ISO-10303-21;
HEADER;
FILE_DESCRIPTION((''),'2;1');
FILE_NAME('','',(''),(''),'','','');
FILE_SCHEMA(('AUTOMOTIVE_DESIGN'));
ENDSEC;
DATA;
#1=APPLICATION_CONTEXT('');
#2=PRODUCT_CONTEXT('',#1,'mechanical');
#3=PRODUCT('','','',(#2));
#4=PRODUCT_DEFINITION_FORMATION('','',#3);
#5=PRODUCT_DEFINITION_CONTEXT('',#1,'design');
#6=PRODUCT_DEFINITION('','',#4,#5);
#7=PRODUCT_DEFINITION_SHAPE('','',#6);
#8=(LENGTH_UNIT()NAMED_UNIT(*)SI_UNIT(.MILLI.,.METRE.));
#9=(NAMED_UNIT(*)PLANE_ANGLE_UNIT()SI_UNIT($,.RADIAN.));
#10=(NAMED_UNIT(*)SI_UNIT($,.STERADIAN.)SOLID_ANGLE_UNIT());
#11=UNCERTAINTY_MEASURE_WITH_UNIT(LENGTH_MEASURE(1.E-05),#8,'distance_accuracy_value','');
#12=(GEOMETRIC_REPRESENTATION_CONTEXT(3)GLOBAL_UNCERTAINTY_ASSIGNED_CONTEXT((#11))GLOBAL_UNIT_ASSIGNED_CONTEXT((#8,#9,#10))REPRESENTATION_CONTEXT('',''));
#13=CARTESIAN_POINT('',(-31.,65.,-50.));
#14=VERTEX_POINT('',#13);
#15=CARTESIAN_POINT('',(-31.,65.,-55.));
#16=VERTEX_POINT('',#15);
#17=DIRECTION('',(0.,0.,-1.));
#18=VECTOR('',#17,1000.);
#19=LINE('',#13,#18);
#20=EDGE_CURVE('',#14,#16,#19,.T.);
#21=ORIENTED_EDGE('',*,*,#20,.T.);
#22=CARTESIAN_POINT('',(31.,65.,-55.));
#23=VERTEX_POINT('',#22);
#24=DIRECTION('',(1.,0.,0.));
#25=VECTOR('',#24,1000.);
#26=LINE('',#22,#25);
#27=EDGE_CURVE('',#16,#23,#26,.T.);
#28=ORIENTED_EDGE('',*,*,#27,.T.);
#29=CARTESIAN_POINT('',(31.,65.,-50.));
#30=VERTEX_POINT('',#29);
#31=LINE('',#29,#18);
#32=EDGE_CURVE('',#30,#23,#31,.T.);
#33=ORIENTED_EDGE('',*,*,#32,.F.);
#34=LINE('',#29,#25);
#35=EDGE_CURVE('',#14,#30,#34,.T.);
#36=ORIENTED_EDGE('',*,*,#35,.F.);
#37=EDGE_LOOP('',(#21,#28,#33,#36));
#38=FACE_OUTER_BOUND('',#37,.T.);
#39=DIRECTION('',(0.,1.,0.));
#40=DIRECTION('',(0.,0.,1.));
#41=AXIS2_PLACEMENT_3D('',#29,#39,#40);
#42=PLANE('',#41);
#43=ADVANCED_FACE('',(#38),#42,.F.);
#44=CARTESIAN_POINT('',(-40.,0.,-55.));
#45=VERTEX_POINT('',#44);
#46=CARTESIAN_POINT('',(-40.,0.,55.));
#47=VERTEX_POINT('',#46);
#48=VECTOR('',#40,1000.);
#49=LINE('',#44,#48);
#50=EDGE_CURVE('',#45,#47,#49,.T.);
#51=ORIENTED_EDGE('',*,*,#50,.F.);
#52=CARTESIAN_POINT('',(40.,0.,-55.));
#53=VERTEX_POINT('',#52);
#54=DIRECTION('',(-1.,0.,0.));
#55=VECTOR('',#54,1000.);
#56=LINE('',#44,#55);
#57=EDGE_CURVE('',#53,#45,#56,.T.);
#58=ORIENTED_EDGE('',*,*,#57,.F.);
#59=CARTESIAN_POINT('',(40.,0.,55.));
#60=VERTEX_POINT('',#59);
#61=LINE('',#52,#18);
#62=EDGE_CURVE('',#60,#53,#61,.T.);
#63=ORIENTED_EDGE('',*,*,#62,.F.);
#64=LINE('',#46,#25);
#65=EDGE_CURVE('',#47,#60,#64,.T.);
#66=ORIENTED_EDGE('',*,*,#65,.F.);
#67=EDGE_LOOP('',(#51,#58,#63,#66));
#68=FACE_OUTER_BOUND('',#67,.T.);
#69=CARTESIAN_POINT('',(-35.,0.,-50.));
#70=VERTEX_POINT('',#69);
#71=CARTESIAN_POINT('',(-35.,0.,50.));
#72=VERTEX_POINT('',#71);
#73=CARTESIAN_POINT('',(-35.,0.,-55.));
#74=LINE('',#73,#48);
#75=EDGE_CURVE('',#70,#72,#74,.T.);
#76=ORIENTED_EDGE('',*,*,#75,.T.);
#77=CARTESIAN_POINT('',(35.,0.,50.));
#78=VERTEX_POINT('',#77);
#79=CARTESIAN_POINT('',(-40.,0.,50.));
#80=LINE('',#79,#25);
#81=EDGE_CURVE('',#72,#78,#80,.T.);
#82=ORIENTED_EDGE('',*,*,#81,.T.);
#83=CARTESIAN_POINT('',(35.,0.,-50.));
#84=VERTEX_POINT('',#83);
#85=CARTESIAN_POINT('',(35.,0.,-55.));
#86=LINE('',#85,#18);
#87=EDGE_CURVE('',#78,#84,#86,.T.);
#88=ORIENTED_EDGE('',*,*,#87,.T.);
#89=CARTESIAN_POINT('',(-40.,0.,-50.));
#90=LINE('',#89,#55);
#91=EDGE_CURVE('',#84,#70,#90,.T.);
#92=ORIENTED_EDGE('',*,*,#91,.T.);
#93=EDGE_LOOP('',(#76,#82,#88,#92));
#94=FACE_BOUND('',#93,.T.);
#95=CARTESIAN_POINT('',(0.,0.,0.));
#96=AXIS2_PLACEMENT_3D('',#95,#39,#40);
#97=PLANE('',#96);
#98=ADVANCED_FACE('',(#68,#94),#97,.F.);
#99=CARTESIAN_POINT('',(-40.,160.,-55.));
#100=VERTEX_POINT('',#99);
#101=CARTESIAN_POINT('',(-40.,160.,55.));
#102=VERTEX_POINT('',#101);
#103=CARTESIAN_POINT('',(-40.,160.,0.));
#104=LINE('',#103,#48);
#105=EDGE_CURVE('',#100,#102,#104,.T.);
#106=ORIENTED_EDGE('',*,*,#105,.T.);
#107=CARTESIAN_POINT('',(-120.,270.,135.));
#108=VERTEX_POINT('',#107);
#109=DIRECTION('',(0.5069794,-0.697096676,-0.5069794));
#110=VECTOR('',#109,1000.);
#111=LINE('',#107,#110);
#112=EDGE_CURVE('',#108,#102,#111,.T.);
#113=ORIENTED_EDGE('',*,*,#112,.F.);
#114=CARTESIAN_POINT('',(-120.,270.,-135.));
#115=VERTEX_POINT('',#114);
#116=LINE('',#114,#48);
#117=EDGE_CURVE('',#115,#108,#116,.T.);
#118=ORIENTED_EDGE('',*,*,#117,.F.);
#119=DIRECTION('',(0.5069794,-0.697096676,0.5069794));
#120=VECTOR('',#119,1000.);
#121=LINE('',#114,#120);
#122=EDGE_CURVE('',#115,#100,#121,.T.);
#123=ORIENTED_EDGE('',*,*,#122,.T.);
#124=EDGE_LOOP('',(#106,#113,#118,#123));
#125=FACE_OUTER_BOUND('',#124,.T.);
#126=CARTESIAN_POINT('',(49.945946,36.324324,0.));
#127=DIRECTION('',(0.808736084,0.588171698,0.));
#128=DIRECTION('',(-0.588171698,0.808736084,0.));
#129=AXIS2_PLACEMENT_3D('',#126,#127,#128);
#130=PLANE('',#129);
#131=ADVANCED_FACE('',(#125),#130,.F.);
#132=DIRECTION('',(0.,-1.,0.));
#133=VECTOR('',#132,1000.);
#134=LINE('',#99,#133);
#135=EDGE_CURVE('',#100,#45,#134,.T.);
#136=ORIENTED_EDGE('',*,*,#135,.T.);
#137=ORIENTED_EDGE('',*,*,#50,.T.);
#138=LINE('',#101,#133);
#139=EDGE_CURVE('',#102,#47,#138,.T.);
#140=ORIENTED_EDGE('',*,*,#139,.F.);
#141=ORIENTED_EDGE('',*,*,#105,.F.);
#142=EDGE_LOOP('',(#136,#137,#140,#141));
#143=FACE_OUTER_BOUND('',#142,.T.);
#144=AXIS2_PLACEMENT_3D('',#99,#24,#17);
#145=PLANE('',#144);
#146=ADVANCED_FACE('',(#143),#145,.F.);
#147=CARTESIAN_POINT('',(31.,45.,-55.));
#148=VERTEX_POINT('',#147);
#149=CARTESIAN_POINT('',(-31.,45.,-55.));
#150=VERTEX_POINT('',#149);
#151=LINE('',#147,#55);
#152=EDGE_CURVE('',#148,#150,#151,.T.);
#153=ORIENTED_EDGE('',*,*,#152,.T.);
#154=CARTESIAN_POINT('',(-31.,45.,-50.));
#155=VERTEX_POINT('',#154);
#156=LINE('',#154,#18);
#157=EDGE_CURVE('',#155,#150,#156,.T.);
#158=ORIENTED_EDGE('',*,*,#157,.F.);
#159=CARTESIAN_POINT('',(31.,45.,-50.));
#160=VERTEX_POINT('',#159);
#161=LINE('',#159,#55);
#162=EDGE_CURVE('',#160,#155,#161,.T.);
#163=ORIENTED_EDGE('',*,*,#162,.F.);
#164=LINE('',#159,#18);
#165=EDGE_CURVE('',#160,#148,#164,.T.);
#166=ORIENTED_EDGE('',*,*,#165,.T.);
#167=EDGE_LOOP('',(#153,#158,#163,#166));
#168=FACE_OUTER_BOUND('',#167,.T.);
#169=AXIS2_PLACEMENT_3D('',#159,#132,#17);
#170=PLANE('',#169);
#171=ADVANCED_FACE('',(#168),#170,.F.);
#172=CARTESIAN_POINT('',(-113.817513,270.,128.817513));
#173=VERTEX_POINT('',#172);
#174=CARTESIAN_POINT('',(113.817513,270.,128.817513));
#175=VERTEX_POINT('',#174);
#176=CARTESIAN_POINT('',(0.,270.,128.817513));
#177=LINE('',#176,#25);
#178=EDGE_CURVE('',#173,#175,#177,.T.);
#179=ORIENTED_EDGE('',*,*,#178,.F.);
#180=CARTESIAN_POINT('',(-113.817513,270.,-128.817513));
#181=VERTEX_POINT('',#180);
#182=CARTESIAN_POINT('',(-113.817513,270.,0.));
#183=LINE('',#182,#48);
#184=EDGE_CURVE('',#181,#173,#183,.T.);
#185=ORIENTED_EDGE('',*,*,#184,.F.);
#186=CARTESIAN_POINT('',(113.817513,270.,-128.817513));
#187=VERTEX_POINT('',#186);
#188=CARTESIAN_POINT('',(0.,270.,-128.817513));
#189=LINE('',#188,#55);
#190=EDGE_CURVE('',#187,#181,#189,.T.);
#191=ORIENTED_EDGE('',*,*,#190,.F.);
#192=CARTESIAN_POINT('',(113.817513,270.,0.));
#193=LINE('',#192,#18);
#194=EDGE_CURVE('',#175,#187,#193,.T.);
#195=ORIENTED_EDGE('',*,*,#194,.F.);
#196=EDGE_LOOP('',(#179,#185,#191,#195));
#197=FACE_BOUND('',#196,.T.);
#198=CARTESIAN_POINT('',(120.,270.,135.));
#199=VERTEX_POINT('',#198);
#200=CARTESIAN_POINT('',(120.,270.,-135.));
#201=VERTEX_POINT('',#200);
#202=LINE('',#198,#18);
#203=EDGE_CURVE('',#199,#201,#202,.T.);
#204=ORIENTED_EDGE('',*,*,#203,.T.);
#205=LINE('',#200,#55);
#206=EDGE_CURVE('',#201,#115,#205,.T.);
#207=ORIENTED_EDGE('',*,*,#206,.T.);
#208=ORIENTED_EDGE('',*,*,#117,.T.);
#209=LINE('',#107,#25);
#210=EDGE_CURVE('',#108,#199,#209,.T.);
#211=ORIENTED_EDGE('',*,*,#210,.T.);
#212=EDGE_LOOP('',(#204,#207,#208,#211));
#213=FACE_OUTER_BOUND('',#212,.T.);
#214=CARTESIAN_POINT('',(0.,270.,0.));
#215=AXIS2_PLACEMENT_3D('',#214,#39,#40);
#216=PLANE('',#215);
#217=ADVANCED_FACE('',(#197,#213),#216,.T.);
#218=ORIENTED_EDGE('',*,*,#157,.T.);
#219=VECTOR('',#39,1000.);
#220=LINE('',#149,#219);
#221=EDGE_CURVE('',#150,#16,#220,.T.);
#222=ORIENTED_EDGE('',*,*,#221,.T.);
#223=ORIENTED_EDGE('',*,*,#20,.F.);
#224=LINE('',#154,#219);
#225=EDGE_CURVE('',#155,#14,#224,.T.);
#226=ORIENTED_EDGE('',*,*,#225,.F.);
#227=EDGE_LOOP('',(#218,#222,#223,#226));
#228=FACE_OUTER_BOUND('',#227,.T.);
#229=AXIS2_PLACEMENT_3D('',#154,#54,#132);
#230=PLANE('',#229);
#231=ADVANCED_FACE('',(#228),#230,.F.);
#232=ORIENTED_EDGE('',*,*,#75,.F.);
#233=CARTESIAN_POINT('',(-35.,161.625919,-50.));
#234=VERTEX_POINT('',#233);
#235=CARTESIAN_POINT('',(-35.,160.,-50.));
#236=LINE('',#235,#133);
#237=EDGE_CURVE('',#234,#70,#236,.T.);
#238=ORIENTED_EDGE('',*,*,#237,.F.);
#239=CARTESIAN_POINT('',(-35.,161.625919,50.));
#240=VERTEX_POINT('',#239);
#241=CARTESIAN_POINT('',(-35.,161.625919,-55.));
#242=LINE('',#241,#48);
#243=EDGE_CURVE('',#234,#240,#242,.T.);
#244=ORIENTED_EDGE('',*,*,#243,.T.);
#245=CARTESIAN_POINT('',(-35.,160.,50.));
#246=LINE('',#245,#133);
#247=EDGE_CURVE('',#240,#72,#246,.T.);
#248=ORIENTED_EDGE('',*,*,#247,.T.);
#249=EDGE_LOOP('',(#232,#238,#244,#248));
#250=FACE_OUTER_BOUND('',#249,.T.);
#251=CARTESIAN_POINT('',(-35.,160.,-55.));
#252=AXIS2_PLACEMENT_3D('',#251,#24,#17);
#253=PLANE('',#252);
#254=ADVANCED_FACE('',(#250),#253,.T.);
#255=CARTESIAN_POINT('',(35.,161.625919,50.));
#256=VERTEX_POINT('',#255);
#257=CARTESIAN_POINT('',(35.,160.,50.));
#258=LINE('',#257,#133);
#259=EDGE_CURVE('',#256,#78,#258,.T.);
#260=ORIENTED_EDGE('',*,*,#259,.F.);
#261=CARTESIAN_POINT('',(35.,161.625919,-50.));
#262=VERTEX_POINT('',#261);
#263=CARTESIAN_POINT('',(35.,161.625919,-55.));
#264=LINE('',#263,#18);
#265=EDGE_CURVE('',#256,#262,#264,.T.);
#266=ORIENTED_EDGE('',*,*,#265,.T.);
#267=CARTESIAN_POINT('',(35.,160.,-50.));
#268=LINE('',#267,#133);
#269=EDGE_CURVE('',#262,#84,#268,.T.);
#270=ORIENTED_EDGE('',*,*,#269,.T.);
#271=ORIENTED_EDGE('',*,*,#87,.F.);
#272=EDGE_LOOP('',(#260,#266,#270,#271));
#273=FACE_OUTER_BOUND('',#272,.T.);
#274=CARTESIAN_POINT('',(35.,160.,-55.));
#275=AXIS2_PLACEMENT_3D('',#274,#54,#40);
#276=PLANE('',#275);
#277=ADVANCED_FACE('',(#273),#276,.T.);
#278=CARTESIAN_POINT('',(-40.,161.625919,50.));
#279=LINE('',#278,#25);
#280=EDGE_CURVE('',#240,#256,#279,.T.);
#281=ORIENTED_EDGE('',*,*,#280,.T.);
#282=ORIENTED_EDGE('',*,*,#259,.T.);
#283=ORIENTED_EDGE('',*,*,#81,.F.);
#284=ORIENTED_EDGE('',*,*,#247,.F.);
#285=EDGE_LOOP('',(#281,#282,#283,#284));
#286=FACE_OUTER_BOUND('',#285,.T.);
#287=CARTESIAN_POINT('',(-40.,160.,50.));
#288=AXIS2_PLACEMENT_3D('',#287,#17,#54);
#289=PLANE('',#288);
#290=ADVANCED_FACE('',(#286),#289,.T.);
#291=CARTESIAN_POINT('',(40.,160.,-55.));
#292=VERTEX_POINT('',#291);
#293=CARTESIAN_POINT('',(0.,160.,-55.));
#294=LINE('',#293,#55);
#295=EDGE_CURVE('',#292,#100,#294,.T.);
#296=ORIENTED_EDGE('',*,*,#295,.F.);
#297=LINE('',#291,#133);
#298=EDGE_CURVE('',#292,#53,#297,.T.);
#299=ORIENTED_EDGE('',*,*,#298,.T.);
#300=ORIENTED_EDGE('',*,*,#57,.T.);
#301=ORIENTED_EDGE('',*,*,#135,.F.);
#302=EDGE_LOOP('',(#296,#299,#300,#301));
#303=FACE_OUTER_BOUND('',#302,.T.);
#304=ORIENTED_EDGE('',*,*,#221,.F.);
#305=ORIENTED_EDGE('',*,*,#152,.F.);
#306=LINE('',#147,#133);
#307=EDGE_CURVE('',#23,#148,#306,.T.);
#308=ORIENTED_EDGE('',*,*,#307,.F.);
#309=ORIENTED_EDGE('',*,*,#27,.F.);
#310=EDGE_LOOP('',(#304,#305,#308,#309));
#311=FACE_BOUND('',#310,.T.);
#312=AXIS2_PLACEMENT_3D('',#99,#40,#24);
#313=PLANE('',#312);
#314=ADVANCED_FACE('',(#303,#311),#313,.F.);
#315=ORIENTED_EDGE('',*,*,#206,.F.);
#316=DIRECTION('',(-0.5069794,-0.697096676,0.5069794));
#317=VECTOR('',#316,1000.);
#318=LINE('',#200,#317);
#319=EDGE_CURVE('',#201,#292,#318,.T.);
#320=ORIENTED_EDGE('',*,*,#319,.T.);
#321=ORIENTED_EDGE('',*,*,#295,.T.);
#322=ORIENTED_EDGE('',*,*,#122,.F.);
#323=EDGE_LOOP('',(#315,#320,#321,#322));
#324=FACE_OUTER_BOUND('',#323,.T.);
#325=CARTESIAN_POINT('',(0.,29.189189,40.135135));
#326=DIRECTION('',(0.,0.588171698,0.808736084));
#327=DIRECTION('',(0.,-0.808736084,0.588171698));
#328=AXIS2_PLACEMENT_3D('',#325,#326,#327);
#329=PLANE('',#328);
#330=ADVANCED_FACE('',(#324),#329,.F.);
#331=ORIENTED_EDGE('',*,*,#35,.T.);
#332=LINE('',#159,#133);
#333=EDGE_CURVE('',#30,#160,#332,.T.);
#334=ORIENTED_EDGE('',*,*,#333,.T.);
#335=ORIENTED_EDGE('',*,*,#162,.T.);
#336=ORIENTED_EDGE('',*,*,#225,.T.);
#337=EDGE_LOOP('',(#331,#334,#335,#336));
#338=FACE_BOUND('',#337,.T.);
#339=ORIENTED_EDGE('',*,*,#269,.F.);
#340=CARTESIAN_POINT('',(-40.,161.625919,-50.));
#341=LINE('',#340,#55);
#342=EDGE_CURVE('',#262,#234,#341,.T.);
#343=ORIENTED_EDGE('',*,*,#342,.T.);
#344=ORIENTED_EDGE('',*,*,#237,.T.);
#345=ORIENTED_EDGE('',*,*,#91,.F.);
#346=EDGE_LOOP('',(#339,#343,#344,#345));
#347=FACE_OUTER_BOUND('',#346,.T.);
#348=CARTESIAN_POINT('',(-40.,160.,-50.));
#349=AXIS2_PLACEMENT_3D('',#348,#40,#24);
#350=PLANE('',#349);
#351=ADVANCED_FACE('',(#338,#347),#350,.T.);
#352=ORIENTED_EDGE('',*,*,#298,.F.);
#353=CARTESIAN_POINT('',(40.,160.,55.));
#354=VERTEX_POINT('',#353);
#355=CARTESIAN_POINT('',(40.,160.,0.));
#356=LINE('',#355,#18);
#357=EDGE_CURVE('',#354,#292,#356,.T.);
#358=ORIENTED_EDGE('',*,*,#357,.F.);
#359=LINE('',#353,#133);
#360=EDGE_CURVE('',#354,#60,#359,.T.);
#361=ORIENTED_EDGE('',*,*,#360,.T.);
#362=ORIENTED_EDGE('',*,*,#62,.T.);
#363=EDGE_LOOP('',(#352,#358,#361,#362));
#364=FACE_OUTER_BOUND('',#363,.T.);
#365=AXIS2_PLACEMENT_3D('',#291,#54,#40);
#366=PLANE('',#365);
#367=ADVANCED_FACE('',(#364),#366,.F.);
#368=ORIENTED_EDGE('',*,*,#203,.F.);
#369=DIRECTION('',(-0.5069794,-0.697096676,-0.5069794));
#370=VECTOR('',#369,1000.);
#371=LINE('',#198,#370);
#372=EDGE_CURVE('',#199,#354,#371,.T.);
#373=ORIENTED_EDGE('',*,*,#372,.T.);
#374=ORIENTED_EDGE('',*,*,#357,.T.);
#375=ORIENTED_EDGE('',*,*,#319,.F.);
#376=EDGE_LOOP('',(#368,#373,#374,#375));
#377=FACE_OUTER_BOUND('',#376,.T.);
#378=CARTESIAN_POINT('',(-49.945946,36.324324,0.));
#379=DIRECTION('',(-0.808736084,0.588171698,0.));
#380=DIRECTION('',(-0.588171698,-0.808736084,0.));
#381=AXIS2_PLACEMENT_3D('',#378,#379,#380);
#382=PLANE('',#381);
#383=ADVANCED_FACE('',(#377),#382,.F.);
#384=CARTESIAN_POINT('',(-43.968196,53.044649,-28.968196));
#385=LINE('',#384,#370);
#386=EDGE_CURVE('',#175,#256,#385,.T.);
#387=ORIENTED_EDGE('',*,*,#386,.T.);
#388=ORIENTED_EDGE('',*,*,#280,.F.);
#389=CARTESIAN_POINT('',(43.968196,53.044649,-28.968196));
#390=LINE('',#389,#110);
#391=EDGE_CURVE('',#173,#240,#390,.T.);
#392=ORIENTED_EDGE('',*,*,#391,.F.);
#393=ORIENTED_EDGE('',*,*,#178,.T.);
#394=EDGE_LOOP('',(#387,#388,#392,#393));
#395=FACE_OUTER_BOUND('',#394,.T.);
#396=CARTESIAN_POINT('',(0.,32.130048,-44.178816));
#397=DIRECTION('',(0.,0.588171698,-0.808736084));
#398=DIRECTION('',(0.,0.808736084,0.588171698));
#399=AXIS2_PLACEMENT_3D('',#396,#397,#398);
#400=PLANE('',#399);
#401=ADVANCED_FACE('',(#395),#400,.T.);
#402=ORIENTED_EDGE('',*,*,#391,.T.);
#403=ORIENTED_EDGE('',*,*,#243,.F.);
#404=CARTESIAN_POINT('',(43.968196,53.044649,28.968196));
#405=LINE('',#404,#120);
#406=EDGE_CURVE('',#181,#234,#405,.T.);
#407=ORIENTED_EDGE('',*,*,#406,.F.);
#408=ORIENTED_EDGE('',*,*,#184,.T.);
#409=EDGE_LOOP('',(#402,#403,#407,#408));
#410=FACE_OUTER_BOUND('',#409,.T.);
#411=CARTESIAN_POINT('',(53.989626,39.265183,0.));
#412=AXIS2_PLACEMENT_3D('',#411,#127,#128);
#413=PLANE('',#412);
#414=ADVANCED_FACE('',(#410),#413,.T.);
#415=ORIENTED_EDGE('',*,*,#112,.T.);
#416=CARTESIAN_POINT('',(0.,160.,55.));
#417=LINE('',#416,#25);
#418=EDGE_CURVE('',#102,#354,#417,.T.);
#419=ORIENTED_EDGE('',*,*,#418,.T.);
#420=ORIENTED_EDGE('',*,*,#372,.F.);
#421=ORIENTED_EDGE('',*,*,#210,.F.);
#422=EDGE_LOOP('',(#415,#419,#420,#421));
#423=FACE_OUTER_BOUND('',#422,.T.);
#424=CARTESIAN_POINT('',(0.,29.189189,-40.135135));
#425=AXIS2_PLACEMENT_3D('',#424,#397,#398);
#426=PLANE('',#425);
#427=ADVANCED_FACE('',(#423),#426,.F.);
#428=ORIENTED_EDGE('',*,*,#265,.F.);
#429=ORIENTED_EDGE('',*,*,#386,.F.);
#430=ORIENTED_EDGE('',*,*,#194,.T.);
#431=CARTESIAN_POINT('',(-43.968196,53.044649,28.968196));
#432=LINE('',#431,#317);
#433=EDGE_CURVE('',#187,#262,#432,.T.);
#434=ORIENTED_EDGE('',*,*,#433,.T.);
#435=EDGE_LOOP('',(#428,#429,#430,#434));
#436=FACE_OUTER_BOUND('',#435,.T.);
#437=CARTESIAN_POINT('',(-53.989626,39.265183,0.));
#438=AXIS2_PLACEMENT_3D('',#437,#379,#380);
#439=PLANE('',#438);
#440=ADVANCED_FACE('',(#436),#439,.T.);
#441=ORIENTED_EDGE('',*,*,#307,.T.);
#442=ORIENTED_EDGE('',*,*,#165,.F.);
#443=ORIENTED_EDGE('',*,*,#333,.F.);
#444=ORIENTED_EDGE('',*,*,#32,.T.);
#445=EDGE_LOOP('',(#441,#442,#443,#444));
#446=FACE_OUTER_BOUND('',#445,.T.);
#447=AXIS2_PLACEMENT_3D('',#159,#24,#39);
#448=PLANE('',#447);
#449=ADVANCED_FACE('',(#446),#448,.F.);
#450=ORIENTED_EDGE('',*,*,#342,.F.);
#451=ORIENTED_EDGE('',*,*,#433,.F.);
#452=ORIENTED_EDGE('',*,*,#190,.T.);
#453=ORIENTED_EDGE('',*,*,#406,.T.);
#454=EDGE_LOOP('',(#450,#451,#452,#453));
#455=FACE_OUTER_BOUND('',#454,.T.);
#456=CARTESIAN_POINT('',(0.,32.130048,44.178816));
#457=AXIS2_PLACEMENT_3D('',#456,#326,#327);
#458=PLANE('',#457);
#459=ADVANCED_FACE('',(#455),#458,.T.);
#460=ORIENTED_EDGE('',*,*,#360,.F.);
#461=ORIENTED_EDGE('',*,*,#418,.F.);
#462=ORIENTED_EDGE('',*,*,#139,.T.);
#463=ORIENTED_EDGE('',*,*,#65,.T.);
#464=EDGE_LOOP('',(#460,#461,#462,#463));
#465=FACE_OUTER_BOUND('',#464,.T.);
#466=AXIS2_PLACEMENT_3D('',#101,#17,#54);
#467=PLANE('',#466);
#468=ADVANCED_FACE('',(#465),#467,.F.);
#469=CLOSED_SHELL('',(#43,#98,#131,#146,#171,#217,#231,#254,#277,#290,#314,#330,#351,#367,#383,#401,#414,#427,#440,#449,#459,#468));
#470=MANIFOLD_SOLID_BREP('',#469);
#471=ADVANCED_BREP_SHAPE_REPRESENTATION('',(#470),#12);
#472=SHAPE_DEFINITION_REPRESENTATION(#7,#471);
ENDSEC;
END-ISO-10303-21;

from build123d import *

# Parameters (mm, degrees)
SKETCH_1_W          = 80
SKETCH_1_H          = 110
EXTRUDE_1_DEPTH     = 160
SHELL_1_T           = -5
SKETCH_7_W          = 62
SKETCH_7_H          = 20
CUT_EXTRUDE_3_DEPTH = 5


with BuildPart() as part:
    # 草图1 → 凸台-拉伸1 (new body)
    with BuildSketch(Plane(origin=(0, 0, 0), x_dir=(1, 0, 0), z_dir=(0, 1, 0))):
        Rectangle(SKETCH_1_W, SKETCH_1_H)
    extrude(amount=EXTRUDE_1_DEPTH)

    # 草图3 → 放样1 section 0
    with BuildSketch(Plane(origin=(0, 270, 0), x_dir=(1, 0, 0), z_dir=(0, 1, 0))):
        with BuildLine():
            Line((-120, -135), (120, -135))
            Line((120, -135), (120, 135))
            Line((120, 135), (-120, 135))
            Line((-120, 135), (-120, -135))
        make_face()
    # 草图2 → 放样1 section 1
    with BuildSketch(Plane(origin=(0, 160, 0), x_dir=(1, 0, 0), z_dir=(0, 1, 0))):
        with BuildLine():
            Line((40, -55), (40, 55))
            Line((40, 55), (-40, 55))
            Line((-40, 55), (-40, -55))
            Line((-40, -55), (40, -55))
        make_face()
    loft()

    # 抽壳1
    shell_1_openings = [part.faces().sort_by_distance(p)[0] for p in [
        (0, 270, 0),
        (0, 0, 0),
    ]]
    offset(amount=SHELL_1_T, openings=shell_1_openings, kind=Kind.INTERSECTION)

    # 草图7 → 切除-拉伸3 (cut)
    with BuildSketch(Plane(origin=(0, 0, -55), x_dir=(-1, 0, 0), z_dir=(0, 0, -1))):
        with Locations((0, 55)):
            Rectangle(SKETCH_7_W, SKETCH_7_H)
    extrude(amount=-CUT_EXTRUDE_3_DEPTH, mode=Mode.SUBTRACT)


solid = part.part
